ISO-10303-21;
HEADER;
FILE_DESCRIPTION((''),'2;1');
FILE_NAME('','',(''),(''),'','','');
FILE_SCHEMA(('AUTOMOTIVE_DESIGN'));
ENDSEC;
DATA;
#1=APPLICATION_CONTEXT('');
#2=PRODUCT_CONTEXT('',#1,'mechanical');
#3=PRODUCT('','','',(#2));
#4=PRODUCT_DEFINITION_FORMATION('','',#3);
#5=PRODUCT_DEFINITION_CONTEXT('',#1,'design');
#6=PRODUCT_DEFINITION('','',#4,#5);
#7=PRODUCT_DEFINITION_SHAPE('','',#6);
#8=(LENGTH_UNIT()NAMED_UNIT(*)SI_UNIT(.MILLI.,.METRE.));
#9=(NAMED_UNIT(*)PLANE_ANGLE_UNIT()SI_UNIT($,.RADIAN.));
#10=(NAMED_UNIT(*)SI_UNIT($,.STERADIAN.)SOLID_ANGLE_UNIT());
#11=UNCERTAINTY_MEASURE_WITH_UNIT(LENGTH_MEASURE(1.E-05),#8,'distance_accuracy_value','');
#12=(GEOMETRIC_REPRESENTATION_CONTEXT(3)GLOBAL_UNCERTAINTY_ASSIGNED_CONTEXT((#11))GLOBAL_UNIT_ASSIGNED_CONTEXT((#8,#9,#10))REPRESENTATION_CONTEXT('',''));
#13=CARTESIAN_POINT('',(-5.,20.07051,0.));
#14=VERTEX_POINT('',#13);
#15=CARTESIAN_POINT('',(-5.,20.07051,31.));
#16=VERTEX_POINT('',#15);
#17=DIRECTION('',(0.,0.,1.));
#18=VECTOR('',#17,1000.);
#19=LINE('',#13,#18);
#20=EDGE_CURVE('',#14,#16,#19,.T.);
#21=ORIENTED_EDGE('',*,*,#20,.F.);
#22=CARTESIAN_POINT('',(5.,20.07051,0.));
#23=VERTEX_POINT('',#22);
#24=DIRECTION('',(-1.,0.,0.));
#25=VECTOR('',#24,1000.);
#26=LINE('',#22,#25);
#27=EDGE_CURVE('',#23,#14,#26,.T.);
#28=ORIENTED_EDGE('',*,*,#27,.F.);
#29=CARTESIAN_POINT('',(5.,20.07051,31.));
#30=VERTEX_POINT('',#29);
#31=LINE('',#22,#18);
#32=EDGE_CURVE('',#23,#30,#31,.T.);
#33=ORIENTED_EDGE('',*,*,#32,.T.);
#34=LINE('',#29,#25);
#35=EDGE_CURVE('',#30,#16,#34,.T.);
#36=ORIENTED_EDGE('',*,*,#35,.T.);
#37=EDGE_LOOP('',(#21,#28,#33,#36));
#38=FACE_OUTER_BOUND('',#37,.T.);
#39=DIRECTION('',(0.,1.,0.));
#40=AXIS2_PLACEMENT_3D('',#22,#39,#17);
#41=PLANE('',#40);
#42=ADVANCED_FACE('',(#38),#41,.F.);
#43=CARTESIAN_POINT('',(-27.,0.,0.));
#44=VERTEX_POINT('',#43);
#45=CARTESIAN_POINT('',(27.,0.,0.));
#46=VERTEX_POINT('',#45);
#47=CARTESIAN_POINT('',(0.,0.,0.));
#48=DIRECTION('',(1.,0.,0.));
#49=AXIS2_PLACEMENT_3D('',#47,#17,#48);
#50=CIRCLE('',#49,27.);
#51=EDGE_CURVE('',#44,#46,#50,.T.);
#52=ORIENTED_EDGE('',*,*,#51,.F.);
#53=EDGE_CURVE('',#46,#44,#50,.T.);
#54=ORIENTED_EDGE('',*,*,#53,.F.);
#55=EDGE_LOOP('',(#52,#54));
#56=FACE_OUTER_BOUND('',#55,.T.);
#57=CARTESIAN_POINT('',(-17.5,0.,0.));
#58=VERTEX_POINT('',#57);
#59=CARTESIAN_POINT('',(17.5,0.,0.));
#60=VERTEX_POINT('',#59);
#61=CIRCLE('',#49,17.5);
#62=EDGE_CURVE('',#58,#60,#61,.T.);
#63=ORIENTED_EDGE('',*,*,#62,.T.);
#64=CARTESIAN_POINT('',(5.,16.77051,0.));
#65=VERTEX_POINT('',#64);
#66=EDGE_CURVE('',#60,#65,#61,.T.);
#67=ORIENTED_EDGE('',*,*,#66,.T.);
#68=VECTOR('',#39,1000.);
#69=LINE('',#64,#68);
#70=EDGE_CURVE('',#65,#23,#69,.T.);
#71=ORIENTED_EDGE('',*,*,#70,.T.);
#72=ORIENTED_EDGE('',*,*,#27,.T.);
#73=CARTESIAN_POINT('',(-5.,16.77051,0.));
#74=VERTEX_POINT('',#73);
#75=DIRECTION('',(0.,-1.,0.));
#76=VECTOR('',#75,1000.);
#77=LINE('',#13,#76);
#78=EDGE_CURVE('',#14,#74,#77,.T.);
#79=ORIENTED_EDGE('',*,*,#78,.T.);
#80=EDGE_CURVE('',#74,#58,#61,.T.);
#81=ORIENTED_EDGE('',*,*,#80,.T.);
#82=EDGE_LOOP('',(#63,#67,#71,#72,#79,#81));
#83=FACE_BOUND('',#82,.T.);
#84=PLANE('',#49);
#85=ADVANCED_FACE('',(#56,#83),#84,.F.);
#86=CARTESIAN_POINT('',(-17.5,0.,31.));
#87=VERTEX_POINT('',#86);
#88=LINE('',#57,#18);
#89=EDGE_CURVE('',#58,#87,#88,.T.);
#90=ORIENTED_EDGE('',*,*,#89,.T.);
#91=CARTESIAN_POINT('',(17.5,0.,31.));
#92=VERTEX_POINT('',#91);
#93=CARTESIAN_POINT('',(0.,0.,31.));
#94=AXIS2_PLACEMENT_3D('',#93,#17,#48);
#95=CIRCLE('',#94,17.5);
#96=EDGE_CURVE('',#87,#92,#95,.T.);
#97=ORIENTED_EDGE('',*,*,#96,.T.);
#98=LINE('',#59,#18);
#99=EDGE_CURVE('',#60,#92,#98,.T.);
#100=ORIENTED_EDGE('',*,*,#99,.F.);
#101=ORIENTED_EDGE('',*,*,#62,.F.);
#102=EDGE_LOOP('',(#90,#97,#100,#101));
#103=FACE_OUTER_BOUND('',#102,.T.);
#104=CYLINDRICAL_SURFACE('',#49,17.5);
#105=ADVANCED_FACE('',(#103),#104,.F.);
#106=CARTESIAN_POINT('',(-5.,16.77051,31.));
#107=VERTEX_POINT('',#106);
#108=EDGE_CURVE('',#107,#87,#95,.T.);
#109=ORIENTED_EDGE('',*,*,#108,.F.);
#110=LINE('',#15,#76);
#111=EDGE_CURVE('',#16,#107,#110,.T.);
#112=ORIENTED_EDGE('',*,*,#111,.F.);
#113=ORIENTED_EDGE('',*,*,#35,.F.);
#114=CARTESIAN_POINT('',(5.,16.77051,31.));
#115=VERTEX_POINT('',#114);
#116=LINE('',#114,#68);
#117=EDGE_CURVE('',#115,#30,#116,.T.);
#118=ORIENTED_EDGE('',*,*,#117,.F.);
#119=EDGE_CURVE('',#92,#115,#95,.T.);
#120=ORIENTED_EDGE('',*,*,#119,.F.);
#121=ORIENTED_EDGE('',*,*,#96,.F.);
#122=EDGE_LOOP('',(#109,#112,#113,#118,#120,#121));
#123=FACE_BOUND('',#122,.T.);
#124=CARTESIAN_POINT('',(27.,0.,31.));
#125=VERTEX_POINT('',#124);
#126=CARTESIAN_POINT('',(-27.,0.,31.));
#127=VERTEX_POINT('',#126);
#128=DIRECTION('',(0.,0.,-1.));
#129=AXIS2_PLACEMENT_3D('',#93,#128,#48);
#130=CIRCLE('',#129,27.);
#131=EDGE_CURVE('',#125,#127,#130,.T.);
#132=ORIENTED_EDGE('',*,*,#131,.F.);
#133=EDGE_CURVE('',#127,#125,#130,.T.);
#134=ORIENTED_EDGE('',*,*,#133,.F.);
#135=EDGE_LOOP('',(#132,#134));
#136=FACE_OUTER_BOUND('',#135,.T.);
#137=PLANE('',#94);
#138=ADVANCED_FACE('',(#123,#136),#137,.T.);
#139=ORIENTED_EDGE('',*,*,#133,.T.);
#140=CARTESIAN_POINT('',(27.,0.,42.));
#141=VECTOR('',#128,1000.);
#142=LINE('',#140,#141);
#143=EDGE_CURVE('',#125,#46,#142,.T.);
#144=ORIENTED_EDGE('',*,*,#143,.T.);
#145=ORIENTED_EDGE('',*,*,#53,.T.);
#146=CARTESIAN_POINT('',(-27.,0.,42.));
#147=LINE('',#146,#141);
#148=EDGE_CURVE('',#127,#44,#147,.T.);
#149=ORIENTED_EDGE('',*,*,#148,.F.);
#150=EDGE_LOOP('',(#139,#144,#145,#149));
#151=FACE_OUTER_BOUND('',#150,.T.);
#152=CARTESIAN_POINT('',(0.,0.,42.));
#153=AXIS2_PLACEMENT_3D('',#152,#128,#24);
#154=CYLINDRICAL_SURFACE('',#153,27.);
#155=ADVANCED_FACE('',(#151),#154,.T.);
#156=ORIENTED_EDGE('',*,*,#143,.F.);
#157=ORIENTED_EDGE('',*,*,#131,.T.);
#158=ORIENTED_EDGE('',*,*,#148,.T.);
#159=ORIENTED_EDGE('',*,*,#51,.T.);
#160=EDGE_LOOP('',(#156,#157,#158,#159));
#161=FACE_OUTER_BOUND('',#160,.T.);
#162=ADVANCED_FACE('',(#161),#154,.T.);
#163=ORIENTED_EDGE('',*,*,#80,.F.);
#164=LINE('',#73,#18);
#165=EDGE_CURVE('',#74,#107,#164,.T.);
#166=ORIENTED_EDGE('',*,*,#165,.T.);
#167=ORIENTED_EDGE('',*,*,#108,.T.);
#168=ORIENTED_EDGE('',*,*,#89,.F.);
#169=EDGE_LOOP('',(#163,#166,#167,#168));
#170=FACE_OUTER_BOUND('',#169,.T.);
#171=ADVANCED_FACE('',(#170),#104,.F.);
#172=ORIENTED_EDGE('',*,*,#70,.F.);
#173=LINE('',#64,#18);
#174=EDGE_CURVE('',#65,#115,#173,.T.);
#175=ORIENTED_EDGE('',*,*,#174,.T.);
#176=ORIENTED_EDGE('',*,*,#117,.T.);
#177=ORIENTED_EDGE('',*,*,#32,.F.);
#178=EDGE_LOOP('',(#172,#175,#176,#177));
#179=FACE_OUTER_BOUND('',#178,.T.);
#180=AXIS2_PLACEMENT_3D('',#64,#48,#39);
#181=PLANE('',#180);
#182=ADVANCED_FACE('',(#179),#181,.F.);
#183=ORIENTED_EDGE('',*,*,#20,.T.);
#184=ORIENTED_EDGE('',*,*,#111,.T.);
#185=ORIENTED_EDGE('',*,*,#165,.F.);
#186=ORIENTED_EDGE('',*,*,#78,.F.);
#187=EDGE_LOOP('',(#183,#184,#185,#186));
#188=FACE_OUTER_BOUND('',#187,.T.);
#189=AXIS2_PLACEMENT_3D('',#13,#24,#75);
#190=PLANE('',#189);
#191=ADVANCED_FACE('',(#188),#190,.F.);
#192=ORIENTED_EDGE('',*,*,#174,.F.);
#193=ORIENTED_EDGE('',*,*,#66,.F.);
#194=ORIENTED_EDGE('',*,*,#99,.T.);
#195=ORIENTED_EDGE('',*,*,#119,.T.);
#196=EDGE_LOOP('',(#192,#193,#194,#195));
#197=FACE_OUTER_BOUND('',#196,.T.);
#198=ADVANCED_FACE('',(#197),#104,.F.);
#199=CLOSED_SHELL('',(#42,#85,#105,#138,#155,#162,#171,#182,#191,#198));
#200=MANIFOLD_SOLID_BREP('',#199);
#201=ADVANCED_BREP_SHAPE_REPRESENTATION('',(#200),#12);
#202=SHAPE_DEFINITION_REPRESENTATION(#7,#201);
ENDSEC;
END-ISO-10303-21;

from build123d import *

# Parameters (mm, degrees)
SKETCH_1_R               = 32
EXTRUDE_1_DEPTH          = 31
CUT_EXTRUDE_1_DEPTH      = 55.854352608
PATTERN_CIRCULAR_1_COUNT = 30
CUT_EXTRUDE_2_DEPTH      = 55.792153984
SKETCH_5_OUTSIDE_W       = 85.106
SKETCH_5_OUTSIDE_H       = 84.892
SKETCH_5_OUTSIDE_R       = 27
CUT_EXTRUDE_3_DEPTH      = 42


with BuildPart() as part:
    # 草图1 → 凸台-拉伸1 (new body)
    with BuildSketch(Plane.XY):
        Circle(SKETCH_1_R)
    extrude(amount=EXTRUDE_1_DEPTH)

    # 草图2 → 切除-拉伸1 (cut, through all)
    with BuildSketch(Plane.XY):
        with BuildLine():
            ThreePointArc((0.291117258, 27.498459061), (0, 27.5), (-0.291117258, 27.498459061))
            add(Edge.make_bspline(
                [(-0.291117258, 27.498459061), (-1.016461379, 27.62595034), (-1.020609493, 28.094265272), (-1.11796964, 28.57715803), (-1.139901483, 28.676258475), (-1.166494173, 28.785849819), (-1.198135434, 28.905795984), (-1.235261247, 29.035929815), (-1.278286716, 29.176077028), (-1.327627025, 29.326048954), (-1.383690587, 29.485644922), (-1.446880683, 29.65465171), (-1.517594534, 29.8328439), (-1.596223153, 30.019983966), (-1.683150964, 30.215822454), (-1.778755503, 30.42009815), (-1.883407094, 30.632538255), (-1.99746854, 30.852858572), (-2.121294814, 31.0807637), (-2.255232758, 31.315947232), (-2.399620786, 31.558091968), (-2.554788592, 31.806870128), (-2.721056861, 32.061943577), (-2.89873699, 32.322964055), (-3.088130814, 32.589573415), (-3.289530328, 32.861403867), (-3.503217435, 33.138078232), (-3.729463678, 33.419210196), (-3.968529992, 33.70440458), (-4.220666464, 33.993257607), (-4.486112085, 34.285357181), (-4.765094529, 34.580283169), (-5.057829915, 34.877607694), (-5.364522622, 35.176895427), (-5.685364966, 35.47770389), (-6.137847732, 35.885241657), (-6.490689237, 36.184143062), (-6.732623663, 36.381116246)],
                knots=[0, 0, 0, 0, 0.115323882, 0.12341257, 0.132512303, 0.142623081, 0.153744905, 0.165877774, 0.179021689, 0.193176649, 0.208342655, 0.224519706, 0.241707802, 0.259906945, 0.279117132, 0.299338365, 0.320570644, 0.342813968, 0.366068337, 0.390333752, 0.415610213, 0.441897719, 0.46919627, 0.497505867, 0.52682651, 0.557158198, 0.588500931, 0.62085471, 0.654219534, 0.688595404, 0.723982319, 0.76038028, 0.797789286, 0.836209338, 0.875640435, 0.916082578, 1, 1, 1, 1], degree=3))
            ThreePointArc((-6.732623663, 36.381116246), (0, 36.998835667), (6.732623663, 36.381116246))
            add(Edge.make_bspline(
                [(0.291117258, 27.498459061), (1.016461379, 27.62595034), (1.020609493, 28.094265272), (1.11796964, 28.57715803), (1.139901483, 28.676258475), (1.166494173, 28.785849819), (1.198135434, 28.905795984), (1.235261247, 29.035929815), (1.278286716, 29.176077028), (1.327627025, 29.326048954), (1.383690587, 29.485644922), (1.446880683, 29.65465171), (1.517594534, 29.8328439), (1.596223153, 30.019983966), (1.683150964, 30.215822454), (1.778755503, 30.42009815), (1.883407094, 30.632538255), (1.99746854, 30.852858572), (2.121294814, 31.0807637), (2.255232758, 31.315947232), (2.399620786, 31.558091968), (2.554788592, 31.806870128), (2.721056861, 32.061943577), (2.89873699, 32.322964055), (3.088130814, 32.589573415), (3.289530328, 32.861403867), (3.503217435, 33.138078232), (3.729463678, 33.419210196), (3.968529992, 33.70440458), (4.220666464, 33.993257607), (4.486112085, 34.285357181), (4.765094529, 34.580283169), (5.057829915, 34.877607694), (5.364522622, 35.176895427), (5.685364966, 35.47770389), (6.137847732, 35.885241657), (6.490689237, 36.184143062), (6.732623663, 36.381116246)],
                knots=[0, 0, 0, 0, 0.115323882, 0.12341257, 0.132512303, 0.142623081, 0.153744905, 0.165877774, 0.179021689, 0.193176649, 0.208342655, 0.224519706, 0.241707802, 0.259906945, 0.279117132, 0.299338365, 0.320570644, 0.342813968, 0.366068337, 0.390333752, 0.415610213, 0.441897719, 0.46919627, 0.497505867, 0.52682651, 0.557158198, 0.588500931, 0.62085471, 0.654219534, 0.688595404, 0.723982319, 0.76038028, 0.797789286, 0.836209338, 0.875640435, 0.916082578, 1, 1, 1, 1], degree=3))
        make_face()
    cut_extrude_1 = extrude(amount=CUT_EXTRUDE_1_DEPTH, mode=Mode.SUBTRACT)

    # 阵列(圆周)1: 切除-拉伸1 ×30 about axis
    pattern_circular_1_axis = Axis((0, 0, 31), (0, 0, -1))
    for i in range(1, PATTERN_CIRCULAR_1_COUNT):
        add(cut_extrude_1.rotate(pattern_circular_1_axis, i * 360 / PATTERN_CIRCULAR_1_COUNT), mode=Mode.SUBTRACT)

    # 草图4 → 切除-拉伸2 (cut, through all)
    with BuildSketch(Plane.XY.offset(31)):
        with BuildLine():
            Line((5, 16.770509831), (5, 20.070509831))
            Line((5, 20.070509831), (-5, 20.070509831))
            Line((-5, 20.070509831), (-5, 16.770509831))
            ThreePointArc((-5, 16.770509831), (0, -17.5), (5, 16.770509831))
        make_face()
    extrude(amount=-CUT_EXTRUDE_2_DEPTH, mode=Mode.SUBTRACT)

    # 草图5 outside → 切除-拉伸3 (cut)
    with BuildSketch(Plane.XY):
        Rectangle(SKETCH_5_OUTSIDE_W, SKETCH_5_OUTSIDE_H)
        Circle(SKETCH_5_OUTSIDE_R, mode=Mode.SUBTRACT)
    extrude(amount=CUT_EXTRUDE_3_DEPTH, mode=Mode.SUBTRACT)


solid = part.part
